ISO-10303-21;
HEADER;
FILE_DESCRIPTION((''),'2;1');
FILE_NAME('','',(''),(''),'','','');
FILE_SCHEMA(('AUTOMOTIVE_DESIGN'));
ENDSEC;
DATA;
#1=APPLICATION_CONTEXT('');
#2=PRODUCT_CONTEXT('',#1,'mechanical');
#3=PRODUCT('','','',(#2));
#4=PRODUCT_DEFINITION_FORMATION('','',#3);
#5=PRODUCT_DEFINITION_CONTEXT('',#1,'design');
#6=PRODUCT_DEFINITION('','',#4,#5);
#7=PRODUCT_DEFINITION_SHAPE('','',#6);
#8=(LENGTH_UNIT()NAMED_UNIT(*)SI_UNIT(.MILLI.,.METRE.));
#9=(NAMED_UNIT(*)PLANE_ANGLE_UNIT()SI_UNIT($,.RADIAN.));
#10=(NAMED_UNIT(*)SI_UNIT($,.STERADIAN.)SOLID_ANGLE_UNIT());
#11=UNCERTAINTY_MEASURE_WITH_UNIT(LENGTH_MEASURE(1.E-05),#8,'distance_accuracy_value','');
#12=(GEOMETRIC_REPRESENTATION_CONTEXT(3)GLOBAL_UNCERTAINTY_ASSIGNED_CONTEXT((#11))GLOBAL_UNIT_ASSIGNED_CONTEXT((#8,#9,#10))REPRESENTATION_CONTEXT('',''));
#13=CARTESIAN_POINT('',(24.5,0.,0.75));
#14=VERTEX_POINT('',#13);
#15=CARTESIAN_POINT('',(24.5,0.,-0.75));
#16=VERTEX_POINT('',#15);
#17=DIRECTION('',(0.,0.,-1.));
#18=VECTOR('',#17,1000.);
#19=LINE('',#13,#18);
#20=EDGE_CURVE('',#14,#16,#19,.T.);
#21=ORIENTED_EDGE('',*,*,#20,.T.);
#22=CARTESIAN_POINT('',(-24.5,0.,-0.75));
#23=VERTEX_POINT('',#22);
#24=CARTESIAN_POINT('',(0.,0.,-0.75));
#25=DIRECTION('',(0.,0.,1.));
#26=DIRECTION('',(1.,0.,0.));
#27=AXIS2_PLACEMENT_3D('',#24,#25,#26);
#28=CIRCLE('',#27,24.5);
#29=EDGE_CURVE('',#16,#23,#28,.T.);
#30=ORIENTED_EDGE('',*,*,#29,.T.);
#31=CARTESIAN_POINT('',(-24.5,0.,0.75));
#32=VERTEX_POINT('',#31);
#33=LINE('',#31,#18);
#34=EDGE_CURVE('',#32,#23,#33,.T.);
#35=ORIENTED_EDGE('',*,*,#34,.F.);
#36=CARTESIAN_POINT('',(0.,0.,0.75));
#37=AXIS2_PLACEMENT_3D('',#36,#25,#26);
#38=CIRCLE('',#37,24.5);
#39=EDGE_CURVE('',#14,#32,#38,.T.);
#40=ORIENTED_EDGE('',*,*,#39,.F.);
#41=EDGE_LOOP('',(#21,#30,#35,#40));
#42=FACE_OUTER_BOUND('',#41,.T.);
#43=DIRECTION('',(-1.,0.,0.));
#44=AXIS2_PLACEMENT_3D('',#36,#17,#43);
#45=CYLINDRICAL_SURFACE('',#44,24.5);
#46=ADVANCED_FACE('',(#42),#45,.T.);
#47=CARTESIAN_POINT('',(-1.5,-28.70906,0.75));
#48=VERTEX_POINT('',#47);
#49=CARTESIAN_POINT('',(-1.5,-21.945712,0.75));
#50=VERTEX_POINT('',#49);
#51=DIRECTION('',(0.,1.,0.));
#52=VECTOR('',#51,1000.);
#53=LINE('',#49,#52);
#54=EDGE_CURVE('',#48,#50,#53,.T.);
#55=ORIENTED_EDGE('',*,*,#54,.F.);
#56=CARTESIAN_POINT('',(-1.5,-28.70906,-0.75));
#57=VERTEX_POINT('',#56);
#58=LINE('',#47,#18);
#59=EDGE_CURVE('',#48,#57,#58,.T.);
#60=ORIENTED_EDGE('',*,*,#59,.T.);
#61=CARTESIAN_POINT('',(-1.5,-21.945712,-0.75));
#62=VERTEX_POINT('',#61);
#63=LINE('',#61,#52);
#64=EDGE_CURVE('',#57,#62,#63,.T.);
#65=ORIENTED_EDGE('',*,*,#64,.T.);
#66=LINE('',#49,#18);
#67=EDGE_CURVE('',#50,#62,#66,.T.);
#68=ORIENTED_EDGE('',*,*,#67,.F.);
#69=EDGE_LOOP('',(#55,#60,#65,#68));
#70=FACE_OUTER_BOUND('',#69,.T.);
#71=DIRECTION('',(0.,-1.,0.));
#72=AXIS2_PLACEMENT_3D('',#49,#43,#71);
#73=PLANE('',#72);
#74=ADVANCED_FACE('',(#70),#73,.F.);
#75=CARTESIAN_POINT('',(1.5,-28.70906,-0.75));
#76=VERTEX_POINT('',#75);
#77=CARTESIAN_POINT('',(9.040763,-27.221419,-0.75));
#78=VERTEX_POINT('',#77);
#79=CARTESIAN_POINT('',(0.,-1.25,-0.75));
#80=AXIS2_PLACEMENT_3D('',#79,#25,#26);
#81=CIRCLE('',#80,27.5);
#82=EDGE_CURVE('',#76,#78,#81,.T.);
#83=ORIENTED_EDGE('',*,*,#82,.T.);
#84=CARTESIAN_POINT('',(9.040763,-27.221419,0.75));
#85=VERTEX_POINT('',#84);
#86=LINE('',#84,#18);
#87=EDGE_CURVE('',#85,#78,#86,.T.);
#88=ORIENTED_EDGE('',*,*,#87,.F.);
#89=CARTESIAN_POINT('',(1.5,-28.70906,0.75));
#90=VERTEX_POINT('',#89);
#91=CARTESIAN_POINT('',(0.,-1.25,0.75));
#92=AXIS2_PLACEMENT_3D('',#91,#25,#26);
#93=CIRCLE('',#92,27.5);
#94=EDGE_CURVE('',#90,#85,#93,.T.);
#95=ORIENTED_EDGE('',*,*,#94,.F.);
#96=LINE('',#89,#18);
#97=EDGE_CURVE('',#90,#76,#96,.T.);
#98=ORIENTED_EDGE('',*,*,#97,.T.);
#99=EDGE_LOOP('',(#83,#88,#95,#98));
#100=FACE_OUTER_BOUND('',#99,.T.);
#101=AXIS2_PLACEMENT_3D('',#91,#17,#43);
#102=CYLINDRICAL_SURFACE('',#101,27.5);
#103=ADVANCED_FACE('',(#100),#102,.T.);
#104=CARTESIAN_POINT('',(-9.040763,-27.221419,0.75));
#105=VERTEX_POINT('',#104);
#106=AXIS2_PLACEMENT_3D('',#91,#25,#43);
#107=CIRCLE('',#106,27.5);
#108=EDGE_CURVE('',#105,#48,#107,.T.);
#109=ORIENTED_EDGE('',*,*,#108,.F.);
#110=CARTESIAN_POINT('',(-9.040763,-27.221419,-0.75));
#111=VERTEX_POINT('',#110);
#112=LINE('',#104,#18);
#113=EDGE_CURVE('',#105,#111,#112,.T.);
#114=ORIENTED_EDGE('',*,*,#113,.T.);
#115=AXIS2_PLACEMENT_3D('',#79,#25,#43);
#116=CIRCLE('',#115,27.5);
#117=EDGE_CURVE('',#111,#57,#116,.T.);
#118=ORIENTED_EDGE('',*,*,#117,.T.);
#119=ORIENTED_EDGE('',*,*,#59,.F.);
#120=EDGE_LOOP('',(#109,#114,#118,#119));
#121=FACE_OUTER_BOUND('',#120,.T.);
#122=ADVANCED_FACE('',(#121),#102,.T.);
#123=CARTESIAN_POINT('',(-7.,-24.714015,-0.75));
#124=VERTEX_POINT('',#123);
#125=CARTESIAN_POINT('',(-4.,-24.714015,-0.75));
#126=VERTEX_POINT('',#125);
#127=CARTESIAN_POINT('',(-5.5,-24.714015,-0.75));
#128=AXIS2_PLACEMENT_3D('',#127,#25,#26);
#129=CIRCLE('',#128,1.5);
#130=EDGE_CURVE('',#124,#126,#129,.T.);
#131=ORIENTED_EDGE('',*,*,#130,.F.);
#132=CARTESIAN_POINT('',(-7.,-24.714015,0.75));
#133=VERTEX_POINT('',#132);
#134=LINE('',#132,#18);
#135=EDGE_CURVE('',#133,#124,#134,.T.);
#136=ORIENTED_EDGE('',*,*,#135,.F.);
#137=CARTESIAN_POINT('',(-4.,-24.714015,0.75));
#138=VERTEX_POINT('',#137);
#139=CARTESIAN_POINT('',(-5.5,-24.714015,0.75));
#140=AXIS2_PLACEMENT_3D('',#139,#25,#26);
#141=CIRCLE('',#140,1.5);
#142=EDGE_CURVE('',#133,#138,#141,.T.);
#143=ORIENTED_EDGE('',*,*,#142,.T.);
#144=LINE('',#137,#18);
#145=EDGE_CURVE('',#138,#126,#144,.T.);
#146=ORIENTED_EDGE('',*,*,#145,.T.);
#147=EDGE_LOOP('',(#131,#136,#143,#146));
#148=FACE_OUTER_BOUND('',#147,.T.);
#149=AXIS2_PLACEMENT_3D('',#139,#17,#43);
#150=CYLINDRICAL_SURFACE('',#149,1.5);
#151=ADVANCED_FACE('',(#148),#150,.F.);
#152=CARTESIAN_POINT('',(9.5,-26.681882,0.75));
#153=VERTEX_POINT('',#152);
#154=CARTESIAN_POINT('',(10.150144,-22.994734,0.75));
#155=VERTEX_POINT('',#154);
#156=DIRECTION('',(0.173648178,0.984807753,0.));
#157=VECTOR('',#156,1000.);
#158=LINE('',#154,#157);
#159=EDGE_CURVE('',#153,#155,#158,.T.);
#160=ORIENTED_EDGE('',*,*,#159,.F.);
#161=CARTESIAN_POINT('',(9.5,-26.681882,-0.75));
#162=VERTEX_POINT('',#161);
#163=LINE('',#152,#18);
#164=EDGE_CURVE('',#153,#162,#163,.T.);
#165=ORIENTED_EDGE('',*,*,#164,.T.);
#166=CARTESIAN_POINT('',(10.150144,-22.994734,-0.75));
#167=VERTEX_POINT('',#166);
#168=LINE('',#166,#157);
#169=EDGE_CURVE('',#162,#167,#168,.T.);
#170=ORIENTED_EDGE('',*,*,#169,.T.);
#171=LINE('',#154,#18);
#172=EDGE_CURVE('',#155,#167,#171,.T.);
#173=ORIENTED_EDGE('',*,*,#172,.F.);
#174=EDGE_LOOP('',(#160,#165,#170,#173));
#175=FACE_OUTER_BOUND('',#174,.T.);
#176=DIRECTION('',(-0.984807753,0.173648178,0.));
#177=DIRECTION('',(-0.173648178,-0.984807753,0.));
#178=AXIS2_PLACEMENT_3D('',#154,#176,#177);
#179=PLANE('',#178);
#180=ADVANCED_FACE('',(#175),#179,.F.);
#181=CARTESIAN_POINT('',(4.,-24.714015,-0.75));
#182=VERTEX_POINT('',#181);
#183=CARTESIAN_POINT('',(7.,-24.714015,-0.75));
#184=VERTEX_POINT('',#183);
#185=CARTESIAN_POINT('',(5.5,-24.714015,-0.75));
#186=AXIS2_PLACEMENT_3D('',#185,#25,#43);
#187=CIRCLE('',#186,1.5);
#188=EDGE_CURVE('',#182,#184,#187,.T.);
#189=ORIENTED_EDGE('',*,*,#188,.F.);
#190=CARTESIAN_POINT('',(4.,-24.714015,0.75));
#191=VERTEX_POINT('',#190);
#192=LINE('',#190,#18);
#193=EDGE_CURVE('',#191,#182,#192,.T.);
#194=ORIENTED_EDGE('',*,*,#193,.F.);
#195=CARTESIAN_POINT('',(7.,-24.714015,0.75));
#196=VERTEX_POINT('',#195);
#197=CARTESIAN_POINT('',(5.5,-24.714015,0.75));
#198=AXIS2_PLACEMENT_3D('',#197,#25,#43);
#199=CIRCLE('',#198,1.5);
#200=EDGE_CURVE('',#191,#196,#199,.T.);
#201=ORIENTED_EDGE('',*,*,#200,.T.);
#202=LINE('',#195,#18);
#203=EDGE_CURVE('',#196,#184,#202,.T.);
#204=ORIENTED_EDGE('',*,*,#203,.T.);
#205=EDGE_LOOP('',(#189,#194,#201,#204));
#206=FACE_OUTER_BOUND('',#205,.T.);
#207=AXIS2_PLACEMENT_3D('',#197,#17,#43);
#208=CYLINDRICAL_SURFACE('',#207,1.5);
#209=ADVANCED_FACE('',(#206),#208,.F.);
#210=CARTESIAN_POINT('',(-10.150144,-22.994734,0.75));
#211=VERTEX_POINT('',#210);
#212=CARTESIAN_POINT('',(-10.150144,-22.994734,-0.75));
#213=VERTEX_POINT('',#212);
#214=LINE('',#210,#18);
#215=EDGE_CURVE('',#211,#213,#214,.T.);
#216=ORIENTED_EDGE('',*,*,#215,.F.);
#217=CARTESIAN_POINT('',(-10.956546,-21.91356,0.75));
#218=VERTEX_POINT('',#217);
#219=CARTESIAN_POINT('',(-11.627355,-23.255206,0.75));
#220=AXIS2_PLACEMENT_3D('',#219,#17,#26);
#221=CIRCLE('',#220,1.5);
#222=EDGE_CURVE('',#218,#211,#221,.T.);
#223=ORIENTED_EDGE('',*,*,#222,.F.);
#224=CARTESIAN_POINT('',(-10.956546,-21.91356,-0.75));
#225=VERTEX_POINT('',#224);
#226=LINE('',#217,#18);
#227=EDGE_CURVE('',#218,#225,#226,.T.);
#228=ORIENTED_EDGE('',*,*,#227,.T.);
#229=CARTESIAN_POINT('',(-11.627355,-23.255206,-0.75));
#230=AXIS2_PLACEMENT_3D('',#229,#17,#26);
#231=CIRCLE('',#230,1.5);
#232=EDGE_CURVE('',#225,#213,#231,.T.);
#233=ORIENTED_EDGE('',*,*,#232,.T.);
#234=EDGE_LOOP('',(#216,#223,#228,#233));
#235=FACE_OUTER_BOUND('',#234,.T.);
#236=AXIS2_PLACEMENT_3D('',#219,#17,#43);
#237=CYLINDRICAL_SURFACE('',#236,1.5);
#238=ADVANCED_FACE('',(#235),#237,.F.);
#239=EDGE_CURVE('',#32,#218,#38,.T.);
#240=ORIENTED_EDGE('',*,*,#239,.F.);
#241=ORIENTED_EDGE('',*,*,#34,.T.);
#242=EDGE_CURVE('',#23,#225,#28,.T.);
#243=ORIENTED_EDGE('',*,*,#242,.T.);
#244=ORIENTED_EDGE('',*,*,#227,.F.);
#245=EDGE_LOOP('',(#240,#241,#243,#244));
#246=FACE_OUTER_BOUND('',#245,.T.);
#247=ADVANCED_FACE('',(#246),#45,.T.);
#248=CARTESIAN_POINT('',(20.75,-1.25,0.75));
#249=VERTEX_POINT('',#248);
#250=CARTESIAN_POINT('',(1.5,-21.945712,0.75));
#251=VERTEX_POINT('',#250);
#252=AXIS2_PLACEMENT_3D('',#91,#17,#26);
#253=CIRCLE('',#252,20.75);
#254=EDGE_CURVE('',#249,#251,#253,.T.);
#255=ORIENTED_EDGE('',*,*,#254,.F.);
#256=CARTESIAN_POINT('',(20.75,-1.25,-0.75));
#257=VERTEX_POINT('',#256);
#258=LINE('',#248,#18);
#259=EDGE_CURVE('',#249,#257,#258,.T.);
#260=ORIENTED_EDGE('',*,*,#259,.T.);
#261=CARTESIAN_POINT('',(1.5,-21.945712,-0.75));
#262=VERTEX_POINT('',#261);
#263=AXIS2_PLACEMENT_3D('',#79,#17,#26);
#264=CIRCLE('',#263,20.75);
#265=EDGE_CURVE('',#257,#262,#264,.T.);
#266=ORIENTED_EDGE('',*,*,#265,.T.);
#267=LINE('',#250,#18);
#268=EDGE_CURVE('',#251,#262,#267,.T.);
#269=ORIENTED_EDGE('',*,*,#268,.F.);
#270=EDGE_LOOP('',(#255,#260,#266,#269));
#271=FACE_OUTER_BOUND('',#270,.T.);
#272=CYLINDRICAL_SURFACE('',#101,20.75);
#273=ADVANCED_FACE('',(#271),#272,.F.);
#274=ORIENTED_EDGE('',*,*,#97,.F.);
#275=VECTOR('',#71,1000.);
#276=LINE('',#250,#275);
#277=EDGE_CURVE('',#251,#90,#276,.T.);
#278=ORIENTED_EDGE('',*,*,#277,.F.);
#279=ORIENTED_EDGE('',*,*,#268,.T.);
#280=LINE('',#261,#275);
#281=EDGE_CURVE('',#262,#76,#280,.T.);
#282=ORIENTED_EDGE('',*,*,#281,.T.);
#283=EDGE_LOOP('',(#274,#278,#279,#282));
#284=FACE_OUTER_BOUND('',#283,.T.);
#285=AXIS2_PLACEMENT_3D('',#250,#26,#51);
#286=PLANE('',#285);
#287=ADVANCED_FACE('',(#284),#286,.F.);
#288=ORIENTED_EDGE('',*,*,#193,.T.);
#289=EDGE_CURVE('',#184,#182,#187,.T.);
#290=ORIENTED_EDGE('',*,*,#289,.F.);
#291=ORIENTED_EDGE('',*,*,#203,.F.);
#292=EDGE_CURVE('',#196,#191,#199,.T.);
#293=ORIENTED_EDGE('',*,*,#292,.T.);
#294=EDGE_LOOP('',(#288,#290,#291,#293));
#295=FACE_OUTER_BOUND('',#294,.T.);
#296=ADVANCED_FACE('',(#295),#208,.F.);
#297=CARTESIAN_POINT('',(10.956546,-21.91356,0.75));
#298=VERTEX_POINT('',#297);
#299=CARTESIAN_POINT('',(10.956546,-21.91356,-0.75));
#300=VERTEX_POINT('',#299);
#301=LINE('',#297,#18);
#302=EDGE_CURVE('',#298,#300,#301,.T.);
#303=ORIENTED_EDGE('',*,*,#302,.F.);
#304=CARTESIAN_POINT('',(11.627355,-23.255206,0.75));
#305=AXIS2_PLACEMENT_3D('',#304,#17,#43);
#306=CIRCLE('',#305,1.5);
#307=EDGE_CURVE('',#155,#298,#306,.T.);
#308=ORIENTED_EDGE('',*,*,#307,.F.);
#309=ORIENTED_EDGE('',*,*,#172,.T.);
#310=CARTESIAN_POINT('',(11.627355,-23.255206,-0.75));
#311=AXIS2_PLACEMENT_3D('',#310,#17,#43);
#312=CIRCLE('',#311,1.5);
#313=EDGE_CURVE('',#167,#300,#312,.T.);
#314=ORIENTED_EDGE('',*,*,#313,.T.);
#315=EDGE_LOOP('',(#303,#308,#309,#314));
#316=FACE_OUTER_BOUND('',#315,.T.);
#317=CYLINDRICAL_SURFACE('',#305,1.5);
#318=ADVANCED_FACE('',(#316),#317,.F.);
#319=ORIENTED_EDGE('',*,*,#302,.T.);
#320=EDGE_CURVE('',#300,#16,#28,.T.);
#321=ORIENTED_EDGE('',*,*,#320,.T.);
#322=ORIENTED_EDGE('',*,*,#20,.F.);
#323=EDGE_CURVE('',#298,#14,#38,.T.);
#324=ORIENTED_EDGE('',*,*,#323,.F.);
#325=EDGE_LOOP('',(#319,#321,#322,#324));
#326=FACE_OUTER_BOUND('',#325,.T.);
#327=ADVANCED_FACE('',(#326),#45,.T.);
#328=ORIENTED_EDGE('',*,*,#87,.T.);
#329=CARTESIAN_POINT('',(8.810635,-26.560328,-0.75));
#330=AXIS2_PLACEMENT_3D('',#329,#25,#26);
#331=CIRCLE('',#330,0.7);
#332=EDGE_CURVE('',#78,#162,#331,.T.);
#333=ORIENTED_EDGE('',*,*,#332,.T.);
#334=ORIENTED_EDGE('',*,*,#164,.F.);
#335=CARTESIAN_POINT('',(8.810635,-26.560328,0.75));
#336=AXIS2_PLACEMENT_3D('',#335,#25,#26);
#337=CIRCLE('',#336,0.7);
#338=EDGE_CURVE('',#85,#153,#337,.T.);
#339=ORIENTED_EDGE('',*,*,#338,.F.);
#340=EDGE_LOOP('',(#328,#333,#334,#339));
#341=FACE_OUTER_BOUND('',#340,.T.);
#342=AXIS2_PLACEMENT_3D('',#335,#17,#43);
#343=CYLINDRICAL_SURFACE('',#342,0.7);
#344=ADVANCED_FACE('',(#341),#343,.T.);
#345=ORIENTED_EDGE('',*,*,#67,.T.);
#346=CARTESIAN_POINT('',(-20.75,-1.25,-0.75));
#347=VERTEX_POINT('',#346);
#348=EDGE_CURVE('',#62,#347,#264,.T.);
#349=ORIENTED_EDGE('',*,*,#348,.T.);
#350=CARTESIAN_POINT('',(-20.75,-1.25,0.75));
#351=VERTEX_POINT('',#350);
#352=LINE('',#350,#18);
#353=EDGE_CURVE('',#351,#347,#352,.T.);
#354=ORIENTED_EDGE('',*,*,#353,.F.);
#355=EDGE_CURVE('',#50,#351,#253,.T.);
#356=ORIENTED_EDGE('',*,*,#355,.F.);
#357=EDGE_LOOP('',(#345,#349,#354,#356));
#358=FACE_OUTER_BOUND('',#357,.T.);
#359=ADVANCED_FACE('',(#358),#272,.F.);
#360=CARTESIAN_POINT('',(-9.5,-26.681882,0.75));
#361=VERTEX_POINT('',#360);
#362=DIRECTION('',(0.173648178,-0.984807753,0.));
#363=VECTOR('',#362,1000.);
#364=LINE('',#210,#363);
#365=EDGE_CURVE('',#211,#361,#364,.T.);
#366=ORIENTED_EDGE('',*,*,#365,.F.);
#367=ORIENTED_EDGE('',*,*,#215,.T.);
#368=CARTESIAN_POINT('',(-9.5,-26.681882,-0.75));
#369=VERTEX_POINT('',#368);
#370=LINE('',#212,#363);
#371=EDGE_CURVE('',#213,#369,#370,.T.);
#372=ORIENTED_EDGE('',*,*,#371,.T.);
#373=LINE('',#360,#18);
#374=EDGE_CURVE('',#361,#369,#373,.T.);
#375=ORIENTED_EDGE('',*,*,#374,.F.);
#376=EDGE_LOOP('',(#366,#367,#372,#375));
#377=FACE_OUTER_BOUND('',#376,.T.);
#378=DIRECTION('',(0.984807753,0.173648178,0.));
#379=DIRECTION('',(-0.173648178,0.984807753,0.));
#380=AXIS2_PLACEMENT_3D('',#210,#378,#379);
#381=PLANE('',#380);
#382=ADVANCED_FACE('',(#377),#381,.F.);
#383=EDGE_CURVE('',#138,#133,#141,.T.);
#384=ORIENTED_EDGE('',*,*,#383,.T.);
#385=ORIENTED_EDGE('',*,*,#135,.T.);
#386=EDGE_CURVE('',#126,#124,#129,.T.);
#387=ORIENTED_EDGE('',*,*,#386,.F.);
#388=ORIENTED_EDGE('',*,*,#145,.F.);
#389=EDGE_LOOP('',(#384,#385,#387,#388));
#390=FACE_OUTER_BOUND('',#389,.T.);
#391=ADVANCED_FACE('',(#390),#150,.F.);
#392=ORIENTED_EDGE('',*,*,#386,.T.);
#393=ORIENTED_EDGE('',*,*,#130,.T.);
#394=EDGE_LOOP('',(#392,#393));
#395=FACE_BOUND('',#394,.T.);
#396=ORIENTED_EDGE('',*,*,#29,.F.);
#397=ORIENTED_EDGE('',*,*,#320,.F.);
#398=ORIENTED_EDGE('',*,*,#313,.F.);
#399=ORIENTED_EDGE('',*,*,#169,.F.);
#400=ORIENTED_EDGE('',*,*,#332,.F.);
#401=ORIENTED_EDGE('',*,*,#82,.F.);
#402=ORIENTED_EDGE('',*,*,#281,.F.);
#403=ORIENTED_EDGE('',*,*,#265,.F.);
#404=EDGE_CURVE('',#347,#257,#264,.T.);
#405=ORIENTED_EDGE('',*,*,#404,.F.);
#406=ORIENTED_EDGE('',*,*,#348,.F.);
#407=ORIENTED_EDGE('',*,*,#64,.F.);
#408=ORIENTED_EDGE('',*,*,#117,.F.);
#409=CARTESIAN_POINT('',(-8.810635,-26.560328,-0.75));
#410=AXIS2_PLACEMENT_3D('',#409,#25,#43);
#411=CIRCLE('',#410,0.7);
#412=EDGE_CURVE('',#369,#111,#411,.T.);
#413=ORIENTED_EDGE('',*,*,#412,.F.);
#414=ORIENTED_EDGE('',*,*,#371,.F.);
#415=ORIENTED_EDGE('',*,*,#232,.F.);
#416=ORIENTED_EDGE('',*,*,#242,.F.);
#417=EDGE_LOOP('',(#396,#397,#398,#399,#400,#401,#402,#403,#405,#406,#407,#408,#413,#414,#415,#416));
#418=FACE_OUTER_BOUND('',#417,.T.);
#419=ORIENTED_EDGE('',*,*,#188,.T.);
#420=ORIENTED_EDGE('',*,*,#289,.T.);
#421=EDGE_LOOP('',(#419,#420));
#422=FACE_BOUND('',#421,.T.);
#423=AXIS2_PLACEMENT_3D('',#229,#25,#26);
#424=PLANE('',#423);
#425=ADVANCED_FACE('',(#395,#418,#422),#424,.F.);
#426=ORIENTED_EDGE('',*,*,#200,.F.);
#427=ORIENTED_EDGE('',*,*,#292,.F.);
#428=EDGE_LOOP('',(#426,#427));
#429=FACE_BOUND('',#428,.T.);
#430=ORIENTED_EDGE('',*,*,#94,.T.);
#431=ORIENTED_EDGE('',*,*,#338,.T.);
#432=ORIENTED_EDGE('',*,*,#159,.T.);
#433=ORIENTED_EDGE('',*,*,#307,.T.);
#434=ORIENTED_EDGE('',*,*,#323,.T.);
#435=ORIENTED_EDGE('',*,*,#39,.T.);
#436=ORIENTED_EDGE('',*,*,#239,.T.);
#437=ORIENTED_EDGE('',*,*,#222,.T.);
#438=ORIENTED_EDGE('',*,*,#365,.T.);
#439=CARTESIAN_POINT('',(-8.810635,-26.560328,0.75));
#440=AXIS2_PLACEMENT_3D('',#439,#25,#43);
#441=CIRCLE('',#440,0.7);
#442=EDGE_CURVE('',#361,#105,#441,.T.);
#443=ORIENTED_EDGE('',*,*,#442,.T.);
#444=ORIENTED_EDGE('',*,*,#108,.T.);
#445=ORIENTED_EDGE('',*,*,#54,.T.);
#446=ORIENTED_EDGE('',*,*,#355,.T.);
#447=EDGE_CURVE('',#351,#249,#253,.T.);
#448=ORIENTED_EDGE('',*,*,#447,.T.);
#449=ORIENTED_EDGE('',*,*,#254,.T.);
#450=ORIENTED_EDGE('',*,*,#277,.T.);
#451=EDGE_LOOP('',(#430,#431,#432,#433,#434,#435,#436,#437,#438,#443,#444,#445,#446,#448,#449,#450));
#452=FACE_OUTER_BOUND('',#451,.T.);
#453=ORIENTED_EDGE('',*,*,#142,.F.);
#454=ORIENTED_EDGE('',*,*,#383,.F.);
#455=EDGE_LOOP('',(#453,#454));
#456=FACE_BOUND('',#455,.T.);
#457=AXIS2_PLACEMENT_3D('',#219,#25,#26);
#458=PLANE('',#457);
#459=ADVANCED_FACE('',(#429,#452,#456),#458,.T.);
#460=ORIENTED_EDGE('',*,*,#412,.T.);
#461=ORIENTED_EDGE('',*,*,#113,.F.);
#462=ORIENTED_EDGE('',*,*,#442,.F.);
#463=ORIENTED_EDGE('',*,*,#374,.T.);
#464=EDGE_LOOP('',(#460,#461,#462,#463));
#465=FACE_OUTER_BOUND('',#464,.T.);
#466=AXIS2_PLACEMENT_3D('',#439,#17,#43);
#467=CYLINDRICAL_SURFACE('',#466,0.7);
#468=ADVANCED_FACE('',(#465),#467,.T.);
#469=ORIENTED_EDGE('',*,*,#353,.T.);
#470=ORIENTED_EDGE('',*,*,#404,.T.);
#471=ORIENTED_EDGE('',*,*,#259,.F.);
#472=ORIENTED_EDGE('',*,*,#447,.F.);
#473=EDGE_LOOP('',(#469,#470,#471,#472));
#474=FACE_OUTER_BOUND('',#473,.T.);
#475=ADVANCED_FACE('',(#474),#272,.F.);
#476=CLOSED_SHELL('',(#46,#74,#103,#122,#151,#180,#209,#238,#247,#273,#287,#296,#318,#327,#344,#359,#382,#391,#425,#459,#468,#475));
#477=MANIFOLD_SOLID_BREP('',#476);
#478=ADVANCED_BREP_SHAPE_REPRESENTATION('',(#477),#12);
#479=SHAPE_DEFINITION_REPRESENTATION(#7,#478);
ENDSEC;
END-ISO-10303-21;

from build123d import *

# Parameters (mm, degrees)
EXTRUDE_972_DEPTH      = 0.75
EXTRUDE_972_DEPTH_BACK = 0.75
SKETCH_1_R             = 1.5


with BuildPart() as part:
    # 草图1 → Extrude 972 (new, two sides: drawn at the far end of the back side and taken through both)
    with BuildSketch(Plane.XY.offset(-EXTRUDE_972_DEPTH_BACK)):
        with BuildLine():
            Line((-1.5, -21.945712116), (-1.5, -28.709060435))
            ThreePointArc((-1.5, -28.709060435), (-5.322611287, -28.229989049), (-9.040763088, -27.22141896))
            ThreePointArc((-9.040763088, -27.22141896), (-9.343684575, -27.01404373), (-9.5, -26.68188202))
            Line((-9.5, -26.68188202), (-10.150143719, -22.994733766))
            ThreePointArc((-10.150143719, -22.994733766), (-10.42496916, -22.358396436), (-10.956546386, -21.91355953))
            ThreePointArc((-10.956546386, -21.91355953), (0, 24.5), (10.956546386, -21.91355953))
            ThreePointArc((10.956546386, -21.91355953), (10.42496916, -22.358396436), (10.150143719, -22.994733766))
            Line((10.150143719, -22.994733766), (9.5, -26.68188202))
            ThreePointArc((9.5, -26.68188202), (9.343684575, -27.01404373), (9.040763088, -27.22141896))
            ThreePointArc((9.040763088, -27.22141896), (5.322611287, -28.229989049), (1.5, -28.709060435))
            Line((1.5, -28.709060435), (1.5, -21.945712116))
            ThreePointArc((1.5, -21.945712116), (0, 19.5), (-1.5, -21.945712116))
        make_face()
        with Locations((-5.5, -24.714015002)):
            Circle(SKETCH_1_R, mode=Mode.SUBTRACT)
        with Locations(Location((5.5, -24.714015002, 0), (0, 0, 180))):
            Circle(SKETCH_1_R, mode=Mode.SUBTRACT)
    extrude(amount=EXTRUDE_972_DEPTH + EXTRUDE_972_DEPTH_BACK)


solid = part.part
